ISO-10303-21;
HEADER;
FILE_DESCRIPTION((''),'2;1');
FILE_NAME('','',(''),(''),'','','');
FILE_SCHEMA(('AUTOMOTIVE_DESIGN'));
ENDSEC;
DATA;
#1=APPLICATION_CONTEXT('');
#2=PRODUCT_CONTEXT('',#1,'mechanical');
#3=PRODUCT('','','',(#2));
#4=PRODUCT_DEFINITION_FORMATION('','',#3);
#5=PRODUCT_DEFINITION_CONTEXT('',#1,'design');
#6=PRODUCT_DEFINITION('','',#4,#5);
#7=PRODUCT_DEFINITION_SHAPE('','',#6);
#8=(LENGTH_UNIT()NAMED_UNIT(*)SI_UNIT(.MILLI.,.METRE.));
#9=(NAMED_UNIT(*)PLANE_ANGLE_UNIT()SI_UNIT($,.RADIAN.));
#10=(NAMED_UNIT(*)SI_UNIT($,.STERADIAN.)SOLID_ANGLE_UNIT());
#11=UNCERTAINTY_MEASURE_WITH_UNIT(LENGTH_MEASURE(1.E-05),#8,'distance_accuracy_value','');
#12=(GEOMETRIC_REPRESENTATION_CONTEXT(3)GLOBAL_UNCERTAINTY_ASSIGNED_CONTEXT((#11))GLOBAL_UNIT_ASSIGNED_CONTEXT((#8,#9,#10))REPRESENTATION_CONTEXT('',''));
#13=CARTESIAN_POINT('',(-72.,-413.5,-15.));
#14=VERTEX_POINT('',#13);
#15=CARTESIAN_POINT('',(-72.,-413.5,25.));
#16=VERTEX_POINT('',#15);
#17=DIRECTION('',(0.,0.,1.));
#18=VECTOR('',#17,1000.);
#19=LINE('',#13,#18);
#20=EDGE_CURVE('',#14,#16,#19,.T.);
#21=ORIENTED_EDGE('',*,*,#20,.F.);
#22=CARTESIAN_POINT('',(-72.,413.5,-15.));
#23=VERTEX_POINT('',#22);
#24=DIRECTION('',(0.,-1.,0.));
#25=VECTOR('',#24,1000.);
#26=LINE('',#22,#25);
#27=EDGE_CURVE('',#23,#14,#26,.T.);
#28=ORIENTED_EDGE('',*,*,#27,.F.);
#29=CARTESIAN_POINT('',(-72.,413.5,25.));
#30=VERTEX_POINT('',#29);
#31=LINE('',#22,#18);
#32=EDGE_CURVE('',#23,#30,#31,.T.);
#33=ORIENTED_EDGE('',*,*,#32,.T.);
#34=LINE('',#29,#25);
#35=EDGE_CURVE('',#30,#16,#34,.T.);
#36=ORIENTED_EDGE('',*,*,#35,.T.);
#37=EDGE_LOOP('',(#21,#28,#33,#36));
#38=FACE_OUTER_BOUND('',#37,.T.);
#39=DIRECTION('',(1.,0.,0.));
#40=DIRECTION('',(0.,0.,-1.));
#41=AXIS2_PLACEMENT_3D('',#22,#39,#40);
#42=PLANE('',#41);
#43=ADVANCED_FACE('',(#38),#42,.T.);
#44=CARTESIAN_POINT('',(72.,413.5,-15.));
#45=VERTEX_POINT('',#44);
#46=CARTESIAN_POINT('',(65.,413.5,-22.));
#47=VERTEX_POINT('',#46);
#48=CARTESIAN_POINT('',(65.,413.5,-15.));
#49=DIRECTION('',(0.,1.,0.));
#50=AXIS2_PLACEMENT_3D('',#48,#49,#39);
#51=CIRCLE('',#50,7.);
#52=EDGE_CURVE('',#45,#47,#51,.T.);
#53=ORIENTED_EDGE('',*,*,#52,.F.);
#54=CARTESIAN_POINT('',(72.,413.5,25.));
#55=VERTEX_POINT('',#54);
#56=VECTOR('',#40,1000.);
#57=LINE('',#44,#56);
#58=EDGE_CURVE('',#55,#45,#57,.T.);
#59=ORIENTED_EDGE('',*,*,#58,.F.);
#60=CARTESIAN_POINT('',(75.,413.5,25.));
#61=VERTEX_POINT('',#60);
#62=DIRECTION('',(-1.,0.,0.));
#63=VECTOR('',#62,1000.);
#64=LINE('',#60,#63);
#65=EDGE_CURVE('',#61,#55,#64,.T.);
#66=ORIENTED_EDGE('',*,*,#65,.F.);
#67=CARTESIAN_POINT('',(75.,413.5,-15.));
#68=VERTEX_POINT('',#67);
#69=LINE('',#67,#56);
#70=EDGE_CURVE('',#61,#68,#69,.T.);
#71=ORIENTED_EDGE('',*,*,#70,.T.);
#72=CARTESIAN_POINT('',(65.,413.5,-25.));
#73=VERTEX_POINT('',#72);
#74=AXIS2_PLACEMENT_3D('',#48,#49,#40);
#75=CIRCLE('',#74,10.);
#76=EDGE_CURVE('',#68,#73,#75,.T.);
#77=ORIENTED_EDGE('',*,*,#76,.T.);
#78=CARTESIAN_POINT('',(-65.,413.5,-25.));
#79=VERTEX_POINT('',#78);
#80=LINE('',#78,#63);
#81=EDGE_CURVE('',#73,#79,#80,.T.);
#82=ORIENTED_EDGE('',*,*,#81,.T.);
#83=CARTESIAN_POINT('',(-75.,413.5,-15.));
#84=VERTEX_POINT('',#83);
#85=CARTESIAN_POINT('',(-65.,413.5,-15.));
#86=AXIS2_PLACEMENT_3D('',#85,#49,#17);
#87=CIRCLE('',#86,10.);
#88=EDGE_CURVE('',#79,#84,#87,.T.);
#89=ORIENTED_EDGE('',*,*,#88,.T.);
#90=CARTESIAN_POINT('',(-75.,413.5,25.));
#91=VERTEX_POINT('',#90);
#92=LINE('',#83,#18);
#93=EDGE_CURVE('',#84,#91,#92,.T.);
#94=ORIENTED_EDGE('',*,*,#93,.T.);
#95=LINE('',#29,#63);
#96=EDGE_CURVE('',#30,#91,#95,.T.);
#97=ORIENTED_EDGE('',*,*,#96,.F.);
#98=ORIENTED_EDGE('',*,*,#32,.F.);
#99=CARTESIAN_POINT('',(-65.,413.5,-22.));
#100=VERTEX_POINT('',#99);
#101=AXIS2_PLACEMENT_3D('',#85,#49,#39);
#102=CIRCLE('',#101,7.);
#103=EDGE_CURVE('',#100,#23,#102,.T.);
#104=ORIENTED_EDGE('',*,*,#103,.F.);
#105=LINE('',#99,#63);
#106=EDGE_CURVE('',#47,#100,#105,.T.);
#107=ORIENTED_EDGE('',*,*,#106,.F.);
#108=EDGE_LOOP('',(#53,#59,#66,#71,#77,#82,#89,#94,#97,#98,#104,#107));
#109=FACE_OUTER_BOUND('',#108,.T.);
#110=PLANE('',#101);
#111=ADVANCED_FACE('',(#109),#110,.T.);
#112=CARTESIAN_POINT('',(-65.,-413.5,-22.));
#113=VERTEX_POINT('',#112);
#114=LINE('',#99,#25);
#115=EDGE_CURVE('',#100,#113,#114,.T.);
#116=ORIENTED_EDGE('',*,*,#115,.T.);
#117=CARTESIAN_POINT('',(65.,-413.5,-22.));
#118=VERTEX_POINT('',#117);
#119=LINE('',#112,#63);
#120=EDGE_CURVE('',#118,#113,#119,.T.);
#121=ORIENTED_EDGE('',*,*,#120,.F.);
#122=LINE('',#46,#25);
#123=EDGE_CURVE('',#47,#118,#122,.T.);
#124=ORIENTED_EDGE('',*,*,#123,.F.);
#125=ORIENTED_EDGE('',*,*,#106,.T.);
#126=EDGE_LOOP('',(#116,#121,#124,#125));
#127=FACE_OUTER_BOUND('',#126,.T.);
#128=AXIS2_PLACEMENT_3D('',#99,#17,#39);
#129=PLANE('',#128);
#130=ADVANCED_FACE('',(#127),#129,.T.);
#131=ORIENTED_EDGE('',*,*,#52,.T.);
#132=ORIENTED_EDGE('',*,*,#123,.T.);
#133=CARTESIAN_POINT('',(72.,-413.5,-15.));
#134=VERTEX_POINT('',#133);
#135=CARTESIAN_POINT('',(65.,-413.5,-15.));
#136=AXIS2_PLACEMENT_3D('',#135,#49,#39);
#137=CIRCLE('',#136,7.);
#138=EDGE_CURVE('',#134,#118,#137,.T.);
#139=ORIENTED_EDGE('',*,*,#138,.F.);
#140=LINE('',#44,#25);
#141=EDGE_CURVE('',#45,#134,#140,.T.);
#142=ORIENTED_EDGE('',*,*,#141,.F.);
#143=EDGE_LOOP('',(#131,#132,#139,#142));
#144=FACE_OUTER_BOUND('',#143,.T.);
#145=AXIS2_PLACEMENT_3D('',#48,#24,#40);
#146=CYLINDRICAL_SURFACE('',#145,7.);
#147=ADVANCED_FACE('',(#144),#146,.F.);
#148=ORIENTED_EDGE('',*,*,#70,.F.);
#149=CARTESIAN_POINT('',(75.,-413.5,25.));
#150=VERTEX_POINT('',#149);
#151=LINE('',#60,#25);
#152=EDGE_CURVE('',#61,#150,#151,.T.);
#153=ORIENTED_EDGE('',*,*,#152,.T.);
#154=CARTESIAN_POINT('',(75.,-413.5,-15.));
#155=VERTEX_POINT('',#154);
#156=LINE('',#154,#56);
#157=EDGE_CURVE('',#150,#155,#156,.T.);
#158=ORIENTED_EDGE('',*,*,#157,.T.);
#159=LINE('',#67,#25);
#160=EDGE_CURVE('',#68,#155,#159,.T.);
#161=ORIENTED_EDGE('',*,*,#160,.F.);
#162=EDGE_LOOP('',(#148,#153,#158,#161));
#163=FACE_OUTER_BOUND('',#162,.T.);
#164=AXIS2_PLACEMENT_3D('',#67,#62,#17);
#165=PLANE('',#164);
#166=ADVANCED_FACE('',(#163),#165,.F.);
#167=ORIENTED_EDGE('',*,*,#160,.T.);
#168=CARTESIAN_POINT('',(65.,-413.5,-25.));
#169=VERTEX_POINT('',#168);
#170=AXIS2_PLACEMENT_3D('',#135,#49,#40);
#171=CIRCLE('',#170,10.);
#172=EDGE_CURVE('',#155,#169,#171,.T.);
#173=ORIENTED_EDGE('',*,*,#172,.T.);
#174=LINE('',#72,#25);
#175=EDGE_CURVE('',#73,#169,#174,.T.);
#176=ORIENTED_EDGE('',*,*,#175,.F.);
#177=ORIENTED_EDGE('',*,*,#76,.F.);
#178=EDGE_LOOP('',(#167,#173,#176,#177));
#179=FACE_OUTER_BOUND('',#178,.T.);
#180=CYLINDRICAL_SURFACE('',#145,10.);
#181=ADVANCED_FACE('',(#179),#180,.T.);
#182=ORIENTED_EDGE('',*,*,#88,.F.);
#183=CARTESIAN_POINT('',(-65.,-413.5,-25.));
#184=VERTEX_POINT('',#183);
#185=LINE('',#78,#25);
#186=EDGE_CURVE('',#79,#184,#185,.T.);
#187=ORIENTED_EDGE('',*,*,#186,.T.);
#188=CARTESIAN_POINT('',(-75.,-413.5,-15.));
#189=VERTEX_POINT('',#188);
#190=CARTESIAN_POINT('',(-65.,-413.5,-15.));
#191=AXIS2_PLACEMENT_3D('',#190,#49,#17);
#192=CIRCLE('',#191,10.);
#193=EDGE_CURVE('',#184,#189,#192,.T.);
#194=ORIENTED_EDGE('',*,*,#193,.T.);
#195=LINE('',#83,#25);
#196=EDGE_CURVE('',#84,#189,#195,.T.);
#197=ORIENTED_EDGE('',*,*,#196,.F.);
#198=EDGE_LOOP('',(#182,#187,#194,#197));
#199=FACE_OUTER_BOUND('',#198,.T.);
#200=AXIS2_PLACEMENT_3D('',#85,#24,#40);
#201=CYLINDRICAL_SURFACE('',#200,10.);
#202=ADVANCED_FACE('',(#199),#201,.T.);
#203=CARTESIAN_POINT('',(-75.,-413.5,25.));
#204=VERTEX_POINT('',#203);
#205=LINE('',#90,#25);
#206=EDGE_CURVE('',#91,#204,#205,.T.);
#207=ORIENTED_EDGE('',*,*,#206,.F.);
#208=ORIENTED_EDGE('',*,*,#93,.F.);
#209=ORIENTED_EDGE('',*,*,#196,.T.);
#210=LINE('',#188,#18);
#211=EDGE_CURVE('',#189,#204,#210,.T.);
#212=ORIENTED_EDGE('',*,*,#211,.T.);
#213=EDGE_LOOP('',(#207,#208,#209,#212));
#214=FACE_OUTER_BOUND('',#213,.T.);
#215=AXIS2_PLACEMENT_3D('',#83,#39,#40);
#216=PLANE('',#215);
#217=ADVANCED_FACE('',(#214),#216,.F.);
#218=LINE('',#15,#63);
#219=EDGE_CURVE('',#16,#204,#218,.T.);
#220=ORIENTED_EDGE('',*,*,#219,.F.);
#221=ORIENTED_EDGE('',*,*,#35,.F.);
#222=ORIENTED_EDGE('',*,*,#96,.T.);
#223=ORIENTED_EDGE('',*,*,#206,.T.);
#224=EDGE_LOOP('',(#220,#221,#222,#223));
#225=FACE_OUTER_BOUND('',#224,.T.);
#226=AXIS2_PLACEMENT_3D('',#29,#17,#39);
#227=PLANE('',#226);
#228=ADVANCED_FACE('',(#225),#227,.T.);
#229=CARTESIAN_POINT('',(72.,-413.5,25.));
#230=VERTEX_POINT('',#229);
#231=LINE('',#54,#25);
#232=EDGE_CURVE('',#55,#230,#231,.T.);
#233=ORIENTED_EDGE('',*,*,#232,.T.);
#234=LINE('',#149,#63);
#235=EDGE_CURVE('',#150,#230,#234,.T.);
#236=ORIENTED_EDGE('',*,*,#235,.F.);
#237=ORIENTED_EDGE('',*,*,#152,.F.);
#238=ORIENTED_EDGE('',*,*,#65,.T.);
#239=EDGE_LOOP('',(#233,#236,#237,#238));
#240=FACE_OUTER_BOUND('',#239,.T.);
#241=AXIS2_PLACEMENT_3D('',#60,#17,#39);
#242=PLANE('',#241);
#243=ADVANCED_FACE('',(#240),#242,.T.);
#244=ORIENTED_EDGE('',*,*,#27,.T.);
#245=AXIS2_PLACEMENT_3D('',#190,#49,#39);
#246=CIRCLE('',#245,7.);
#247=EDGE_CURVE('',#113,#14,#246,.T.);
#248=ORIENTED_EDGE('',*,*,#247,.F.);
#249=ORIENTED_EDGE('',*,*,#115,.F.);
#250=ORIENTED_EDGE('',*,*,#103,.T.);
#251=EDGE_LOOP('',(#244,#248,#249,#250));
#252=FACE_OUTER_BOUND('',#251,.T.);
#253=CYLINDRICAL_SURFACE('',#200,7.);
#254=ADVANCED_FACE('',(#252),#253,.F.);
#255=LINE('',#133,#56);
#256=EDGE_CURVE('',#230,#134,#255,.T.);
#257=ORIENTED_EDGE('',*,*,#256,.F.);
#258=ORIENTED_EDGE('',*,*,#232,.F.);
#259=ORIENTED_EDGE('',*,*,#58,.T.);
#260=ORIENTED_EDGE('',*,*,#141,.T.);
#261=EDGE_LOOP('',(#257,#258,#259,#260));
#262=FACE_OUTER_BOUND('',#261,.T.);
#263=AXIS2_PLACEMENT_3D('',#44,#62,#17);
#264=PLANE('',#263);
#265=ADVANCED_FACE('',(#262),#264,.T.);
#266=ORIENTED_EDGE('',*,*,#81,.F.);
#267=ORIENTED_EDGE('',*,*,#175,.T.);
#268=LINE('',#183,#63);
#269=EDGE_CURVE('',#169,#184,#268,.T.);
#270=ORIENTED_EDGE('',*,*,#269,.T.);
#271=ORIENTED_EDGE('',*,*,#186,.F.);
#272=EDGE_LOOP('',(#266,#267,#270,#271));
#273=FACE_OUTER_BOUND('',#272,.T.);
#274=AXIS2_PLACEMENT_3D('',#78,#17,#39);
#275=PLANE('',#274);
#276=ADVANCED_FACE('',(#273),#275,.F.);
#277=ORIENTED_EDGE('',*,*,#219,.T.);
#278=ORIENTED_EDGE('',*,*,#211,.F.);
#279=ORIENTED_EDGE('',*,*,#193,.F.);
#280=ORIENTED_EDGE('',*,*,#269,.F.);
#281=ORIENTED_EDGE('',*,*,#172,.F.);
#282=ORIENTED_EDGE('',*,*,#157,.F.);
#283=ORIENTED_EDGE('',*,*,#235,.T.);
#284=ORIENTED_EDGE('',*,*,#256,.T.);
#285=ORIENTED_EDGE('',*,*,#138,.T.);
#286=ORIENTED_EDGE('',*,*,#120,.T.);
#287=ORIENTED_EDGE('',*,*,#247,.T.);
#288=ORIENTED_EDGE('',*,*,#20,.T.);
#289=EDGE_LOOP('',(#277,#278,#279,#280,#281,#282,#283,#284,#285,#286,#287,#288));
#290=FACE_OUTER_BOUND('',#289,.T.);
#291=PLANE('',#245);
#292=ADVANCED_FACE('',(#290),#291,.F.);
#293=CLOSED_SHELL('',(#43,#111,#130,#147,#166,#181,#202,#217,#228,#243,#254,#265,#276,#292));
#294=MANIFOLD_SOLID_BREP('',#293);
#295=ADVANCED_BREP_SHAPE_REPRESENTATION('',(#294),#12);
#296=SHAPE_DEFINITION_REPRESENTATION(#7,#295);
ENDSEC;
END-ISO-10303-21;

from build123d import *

# Parameters (mm, degrees)
EXTRUDE_THIN1_DEPTH = 413.5


with BuildPart() as part:
    # Sketch1 → Extrude-Thin1 (new, symmetric)
    with BuildSketch(Plane(origin=(0, 0, 0), x_dir=(1, 0, 0), z_dir=(0, 1, 0))):
        with BuildLine():
            Line((-75, -25), (-75, 15))
            ThreePointArc((-75, 15), (-72.071067812, 22.071067812), (-65, 25))
            Line((-65, 25), (65, 25))
            ThreePointArc((65, 25), (72.071067812, 22.071067812), (75, 15))
            Line((75, 15), (75, -25))
            Line((75, -25), (72, -25))
            Line((72, -25), (72, 15))
            ThreePointArc((72, 15), (69.949747468, 19.949747468), (65, 22))
            Line((65, 22), (-65, 22))
            ThreePointArc((-65, 22), (-69.949747468, 19.949747468), (-72, 15))
            Line((-72, 15), (-72, -25))
            Line((-72, -25), (-75, -25))
        make_face()
    extrude(amount=EXTRUDE_THIN1_DEPTH, both=True)


solid = part.part
